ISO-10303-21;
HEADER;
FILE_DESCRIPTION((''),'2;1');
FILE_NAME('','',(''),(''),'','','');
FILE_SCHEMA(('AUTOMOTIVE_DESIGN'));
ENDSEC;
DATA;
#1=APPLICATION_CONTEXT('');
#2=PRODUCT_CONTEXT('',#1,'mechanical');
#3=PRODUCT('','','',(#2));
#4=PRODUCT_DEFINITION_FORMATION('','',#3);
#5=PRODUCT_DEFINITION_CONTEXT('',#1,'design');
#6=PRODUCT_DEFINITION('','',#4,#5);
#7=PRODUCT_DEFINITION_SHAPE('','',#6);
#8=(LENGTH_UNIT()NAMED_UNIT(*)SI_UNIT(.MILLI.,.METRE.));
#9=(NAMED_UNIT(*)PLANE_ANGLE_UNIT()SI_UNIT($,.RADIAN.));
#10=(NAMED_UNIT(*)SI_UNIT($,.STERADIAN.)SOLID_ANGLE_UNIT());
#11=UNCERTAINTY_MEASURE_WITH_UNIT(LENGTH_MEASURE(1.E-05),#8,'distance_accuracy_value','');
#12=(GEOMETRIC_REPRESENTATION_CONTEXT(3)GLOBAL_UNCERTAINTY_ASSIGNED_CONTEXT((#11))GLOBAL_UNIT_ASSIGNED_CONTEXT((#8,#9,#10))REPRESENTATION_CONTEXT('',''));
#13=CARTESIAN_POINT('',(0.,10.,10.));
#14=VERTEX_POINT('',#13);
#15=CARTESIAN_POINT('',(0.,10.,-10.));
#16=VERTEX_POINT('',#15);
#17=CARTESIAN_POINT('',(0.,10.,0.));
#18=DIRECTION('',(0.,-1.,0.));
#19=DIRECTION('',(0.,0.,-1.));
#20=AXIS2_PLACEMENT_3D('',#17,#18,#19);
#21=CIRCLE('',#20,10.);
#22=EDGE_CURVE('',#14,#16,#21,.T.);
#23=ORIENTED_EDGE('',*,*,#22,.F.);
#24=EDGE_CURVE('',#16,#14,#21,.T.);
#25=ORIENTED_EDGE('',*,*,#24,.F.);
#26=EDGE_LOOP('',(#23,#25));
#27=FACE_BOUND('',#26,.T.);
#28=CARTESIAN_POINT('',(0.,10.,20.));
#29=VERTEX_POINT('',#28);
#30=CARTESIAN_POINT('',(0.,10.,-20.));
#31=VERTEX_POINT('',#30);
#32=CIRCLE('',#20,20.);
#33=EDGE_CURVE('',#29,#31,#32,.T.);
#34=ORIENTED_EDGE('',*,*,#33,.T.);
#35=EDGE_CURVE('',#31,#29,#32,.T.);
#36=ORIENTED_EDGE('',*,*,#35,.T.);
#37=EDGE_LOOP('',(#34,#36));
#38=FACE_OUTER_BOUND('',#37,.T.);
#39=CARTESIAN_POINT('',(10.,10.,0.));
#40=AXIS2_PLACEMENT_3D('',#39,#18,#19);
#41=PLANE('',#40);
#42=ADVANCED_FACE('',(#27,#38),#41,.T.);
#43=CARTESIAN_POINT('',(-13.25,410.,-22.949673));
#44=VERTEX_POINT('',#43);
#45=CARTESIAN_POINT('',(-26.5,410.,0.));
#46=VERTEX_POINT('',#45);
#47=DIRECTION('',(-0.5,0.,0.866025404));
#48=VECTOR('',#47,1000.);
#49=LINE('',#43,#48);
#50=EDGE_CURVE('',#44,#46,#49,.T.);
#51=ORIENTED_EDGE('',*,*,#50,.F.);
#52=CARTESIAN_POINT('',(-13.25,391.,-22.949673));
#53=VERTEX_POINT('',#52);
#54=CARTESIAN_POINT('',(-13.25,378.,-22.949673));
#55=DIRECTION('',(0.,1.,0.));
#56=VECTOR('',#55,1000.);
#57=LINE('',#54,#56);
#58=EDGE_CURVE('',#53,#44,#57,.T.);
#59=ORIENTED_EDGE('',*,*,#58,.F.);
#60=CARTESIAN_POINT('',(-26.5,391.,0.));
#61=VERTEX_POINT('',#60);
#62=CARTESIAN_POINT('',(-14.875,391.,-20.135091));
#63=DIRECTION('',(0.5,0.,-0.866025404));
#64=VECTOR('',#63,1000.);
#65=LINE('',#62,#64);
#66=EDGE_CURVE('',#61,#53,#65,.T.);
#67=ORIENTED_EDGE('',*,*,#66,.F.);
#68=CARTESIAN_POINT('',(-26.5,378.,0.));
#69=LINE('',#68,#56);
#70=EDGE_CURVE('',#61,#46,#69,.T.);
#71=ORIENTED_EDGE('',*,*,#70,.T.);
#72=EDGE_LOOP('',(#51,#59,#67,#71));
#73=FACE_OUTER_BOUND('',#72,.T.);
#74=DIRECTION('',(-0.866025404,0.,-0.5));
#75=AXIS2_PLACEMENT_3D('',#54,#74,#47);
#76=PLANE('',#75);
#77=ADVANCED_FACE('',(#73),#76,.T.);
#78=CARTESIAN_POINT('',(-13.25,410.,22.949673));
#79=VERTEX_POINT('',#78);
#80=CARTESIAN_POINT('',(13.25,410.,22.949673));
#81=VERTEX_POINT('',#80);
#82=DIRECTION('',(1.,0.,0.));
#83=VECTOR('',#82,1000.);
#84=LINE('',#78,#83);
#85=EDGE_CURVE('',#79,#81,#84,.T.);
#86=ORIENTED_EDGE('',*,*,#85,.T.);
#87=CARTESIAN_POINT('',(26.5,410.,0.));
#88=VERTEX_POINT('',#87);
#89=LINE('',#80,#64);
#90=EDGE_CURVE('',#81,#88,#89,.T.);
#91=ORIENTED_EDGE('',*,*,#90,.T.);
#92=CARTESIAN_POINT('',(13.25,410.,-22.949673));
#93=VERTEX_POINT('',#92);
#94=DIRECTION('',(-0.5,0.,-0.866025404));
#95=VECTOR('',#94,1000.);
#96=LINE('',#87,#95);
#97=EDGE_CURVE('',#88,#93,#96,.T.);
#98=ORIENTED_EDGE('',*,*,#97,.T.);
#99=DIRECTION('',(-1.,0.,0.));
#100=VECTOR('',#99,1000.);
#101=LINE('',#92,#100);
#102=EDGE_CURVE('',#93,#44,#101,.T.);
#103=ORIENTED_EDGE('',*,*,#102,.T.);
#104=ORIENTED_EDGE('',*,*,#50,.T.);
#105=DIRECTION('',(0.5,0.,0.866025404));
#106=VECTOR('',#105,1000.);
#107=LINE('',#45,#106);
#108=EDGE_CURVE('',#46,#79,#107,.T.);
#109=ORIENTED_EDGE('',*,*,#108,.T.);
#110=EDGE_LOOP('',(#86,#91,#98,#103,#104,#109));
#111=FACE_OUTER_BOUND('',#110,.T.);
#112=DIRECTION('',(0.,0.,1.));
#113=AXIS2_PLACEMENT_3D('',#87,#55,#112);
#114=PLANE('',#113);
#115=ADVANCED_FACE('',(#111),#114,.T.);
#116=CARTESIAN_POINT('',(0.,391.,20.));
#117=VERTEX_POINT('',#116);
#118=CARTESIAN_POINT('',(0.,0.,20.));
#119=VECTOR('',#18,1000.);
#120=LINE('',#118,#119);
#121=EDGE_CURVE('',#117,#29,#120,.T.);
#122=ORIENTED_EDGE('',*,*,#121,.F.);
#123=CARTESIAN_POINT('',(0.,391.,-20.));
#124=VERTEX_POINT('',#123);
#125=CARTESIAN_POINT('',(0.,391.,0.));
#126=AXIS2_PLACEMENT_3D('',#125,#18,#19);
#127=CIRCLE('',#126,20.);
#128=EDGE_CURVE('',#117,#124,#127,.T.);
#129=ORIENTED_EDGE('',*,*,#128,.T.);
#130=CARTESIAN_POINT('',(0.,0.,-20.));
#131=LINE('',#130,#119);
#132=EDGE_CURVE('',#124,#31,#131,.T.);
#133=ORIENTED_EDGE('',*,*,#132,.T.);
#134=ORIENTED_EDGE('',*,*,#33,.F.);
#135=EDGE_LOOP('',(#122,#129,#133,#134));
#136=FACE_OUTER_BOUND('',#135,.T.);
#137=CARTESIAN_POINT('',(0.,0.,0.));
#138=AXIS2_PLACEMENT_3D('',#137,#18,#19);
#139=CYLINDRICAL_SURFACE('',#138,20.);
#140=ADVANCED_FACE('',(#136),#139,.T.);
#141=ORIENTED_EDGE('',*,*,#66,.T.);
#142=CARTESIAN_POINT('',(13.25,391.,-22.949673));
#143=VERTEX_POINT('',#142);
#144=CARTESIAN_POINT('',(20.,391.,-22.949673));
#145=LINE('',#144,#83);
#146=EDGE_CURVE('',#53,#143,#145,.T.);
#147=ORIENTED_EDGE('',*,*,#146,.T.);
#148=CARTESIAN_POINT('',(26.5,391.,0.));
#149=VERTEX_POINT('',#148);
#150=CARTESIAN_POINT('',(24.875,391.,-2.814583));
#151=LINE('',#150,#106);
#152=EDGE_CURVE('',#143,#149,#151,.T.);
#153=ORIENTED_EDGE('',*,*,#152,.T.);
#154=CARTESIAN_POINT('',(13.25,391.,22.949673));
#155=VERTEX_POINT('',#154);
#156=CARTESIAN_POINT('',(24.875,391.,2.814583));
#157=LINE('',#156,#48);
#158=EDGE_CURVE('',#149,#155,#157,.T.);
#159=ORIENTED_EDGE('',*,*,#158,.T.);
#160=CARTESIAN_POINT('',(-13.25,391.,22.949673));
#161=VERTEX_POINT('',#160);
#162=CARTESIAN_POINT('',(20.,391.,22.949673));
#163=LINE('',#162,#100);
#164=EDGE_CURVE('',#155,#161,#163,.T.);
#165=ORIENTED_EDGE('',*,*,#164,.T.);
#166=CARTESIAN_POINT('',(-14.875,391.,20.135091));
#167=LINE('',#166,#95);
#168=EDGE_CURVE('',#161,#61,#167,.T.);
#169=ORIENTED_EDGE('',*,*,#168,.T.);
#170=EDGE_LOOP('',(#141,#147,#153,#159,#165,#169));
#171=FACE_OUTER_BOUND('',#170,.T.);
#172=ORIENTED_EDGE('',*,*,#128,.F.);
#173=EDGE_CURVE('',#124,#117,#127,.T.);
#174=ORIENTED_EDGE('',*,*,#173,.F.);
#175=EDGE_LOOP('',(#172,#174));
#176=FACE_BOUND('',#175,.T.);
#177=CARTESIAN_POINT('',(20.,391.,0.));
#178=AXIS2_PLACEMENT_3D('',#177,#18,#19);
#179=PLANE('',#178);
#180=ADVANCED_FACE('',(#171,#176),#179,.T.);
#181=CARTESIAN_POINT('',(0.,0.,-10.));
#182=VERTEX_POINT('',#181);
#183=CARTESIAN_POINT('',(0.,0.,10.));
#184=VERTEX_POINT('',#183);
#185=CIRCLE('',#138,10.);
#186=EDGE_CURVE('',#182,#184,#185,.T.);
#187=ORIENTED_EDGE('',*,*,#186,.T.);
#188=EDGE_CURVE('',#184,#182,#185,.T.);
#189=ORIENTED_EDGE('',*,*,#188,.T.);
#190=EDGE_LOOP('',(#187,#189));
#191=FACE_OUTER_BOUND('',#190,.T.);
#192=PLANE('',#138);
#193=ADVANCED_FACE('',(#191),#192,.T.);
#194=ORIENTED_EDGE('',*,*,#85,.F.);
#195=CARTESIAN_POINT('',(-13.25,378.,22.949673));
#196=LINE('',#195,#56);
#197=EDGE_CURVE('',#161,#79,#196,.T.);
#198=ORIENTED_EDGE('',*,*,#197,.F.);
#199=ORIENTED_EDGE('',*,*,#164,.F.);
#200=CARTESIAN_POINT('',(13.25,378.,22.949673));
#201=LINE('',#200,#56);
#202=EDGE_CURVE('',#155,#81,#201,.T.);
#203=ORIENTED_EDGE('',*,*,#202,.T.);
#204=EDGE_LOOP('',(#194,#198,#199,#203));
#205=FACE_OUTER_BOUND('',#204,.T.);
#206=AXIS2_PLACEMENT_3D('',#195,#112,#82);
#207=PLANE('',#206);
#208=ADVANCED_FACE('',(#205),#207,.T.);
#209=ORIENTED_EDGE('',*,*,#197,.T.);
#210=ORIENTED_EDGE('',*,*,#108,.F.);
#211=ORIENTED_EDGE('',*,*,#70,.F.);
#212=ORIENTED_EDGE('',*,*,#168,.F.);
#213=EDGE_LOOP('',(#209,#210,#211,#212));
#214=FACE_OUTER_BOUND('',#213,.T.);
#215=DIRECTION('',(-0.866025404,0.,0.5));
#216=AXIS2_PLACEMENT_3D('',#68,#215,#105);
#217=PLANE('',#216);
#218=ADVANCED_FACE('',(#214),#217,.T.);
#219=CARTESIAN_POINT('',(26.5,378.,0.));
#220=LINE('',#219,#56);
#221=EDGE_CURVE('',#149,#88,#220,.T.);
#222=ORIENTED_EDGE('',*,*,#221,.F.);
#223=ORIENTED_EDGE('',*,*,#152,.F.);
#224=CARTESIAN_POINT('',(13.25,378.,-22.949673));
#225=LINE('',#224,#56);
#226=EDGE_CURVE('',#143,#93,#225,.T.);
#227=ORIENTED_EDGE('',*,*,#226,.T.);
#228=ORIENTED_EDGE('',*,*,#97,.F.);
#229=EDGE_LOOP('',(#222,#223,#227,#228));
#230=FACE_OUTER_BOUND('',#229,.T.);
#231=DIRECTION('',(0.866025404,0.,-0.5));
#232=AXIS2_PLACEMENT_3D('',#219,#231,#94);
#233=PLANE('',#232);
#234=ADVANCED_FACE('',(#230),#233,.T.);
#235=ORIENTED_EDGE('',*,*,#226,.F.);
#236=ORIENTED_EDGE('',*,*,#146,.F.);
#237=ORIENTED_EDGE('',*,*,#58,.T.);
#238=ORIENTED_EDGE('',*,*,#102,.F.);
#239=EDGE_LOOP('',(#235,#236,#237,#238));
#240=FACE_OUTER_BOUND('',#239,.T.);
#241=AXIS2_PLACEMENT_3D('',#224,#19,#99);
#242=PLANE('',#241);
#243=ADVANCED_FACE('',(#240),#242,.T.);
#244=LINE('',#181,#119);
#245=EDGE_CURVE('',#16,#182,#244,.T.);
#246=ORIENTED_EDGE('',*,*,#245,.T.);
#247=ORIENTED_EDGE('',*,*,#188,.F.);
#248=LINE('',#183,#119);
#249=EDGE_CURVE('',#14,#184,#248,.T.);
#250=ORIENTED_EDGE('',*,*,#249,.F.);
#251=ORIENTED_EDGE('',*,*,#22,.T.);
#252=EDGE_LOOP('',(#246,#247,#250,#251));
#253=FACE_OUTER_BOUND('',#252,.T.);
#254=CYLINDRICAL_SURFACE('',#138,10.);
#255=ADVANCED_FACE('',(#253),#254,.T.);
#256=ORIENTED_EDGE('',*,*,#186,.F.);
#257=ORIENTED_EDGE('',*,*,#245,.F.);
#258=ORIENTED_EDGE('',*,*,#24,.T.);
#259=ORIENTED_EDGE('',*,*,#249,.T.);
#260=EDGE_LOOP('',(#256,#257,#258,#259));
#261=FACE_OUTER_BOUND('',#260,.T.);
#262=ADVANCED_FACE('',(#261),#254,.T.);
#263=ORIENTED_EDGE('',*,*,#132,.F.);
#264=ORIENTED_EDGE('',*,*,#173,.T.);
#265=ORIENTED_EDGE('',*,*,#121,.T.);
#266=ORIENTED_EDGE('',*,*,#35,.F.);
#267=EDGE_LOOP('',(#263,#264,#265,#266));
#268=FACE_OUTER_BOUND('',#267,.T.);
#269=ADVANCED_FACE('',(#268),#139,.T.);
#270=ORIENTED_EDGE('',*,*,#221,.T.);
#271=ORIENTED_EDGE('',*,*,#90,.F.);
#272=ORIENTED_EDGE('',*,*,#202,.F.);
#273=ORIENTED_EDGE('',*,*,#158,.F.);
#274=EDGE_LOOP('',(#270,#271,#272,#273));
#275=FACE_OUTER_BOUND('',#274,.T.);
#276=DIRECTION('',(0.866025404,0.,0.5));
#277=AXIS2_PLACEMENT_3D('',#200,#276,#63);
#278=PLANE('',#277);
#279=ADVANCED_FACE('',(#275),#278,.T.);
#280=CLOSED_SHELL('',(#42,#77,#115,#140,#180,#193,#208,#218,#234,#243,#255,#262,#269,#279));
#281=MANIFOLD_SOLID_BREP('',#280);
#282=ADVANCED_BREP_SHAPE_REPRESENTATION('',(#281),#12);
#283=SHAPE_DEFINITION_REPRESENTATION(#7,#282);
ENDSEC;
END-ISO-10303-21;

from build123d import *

# Parameters (mm, degrees)
SKETCH2_OUTSIDE_W  = 138.358
SKETCH2_OUTSIDE_H  = 138.358
CUT_EXTRUDE1_DEPTH = 32


with BuildPart() as part:
    # Sketch1 → Revolve1 (revolve)
    with BuildSketch(Plane.XY, mode=Mode.PRIVATE) as revolve1_sk:
        Polygon((0, 0), (10, 0), (10, 10), (20, 10), (20, 391), (26.5, 391), (26.5, 410), (0, 410), align=None)
    revolve(revolve1_sk.sketch.rotate(Axis((0, 0, 0), (0, 1, 0)), 90), axis=Axis((0, 0, 0), (0, 1, 0)))

    # Sketch2 outside → Cut-Extrude1 (cut)
    with BuildSketch(Plane(origin=(0, 410, 0), x_dir=(1, 0, 0), z_dir=(0, 1, 0))):
        Rectangle(SKETCH2_OUTSIDE_W, SKETCH2_OUTSIDE_H)
        Polygon((-26.5, 0), (-13.25, -22.9496732), (13.25, -22.9496732), (26.5, 0), (13.25, 22.9496732), (-13.25, 22.9496732), align=None, mode=Mode.SUBTRACT)
    extrude(amount=-CUT_EXTRUDE1_DEPTH, mode=Mode.SUBTRACT)


solid = part.part
